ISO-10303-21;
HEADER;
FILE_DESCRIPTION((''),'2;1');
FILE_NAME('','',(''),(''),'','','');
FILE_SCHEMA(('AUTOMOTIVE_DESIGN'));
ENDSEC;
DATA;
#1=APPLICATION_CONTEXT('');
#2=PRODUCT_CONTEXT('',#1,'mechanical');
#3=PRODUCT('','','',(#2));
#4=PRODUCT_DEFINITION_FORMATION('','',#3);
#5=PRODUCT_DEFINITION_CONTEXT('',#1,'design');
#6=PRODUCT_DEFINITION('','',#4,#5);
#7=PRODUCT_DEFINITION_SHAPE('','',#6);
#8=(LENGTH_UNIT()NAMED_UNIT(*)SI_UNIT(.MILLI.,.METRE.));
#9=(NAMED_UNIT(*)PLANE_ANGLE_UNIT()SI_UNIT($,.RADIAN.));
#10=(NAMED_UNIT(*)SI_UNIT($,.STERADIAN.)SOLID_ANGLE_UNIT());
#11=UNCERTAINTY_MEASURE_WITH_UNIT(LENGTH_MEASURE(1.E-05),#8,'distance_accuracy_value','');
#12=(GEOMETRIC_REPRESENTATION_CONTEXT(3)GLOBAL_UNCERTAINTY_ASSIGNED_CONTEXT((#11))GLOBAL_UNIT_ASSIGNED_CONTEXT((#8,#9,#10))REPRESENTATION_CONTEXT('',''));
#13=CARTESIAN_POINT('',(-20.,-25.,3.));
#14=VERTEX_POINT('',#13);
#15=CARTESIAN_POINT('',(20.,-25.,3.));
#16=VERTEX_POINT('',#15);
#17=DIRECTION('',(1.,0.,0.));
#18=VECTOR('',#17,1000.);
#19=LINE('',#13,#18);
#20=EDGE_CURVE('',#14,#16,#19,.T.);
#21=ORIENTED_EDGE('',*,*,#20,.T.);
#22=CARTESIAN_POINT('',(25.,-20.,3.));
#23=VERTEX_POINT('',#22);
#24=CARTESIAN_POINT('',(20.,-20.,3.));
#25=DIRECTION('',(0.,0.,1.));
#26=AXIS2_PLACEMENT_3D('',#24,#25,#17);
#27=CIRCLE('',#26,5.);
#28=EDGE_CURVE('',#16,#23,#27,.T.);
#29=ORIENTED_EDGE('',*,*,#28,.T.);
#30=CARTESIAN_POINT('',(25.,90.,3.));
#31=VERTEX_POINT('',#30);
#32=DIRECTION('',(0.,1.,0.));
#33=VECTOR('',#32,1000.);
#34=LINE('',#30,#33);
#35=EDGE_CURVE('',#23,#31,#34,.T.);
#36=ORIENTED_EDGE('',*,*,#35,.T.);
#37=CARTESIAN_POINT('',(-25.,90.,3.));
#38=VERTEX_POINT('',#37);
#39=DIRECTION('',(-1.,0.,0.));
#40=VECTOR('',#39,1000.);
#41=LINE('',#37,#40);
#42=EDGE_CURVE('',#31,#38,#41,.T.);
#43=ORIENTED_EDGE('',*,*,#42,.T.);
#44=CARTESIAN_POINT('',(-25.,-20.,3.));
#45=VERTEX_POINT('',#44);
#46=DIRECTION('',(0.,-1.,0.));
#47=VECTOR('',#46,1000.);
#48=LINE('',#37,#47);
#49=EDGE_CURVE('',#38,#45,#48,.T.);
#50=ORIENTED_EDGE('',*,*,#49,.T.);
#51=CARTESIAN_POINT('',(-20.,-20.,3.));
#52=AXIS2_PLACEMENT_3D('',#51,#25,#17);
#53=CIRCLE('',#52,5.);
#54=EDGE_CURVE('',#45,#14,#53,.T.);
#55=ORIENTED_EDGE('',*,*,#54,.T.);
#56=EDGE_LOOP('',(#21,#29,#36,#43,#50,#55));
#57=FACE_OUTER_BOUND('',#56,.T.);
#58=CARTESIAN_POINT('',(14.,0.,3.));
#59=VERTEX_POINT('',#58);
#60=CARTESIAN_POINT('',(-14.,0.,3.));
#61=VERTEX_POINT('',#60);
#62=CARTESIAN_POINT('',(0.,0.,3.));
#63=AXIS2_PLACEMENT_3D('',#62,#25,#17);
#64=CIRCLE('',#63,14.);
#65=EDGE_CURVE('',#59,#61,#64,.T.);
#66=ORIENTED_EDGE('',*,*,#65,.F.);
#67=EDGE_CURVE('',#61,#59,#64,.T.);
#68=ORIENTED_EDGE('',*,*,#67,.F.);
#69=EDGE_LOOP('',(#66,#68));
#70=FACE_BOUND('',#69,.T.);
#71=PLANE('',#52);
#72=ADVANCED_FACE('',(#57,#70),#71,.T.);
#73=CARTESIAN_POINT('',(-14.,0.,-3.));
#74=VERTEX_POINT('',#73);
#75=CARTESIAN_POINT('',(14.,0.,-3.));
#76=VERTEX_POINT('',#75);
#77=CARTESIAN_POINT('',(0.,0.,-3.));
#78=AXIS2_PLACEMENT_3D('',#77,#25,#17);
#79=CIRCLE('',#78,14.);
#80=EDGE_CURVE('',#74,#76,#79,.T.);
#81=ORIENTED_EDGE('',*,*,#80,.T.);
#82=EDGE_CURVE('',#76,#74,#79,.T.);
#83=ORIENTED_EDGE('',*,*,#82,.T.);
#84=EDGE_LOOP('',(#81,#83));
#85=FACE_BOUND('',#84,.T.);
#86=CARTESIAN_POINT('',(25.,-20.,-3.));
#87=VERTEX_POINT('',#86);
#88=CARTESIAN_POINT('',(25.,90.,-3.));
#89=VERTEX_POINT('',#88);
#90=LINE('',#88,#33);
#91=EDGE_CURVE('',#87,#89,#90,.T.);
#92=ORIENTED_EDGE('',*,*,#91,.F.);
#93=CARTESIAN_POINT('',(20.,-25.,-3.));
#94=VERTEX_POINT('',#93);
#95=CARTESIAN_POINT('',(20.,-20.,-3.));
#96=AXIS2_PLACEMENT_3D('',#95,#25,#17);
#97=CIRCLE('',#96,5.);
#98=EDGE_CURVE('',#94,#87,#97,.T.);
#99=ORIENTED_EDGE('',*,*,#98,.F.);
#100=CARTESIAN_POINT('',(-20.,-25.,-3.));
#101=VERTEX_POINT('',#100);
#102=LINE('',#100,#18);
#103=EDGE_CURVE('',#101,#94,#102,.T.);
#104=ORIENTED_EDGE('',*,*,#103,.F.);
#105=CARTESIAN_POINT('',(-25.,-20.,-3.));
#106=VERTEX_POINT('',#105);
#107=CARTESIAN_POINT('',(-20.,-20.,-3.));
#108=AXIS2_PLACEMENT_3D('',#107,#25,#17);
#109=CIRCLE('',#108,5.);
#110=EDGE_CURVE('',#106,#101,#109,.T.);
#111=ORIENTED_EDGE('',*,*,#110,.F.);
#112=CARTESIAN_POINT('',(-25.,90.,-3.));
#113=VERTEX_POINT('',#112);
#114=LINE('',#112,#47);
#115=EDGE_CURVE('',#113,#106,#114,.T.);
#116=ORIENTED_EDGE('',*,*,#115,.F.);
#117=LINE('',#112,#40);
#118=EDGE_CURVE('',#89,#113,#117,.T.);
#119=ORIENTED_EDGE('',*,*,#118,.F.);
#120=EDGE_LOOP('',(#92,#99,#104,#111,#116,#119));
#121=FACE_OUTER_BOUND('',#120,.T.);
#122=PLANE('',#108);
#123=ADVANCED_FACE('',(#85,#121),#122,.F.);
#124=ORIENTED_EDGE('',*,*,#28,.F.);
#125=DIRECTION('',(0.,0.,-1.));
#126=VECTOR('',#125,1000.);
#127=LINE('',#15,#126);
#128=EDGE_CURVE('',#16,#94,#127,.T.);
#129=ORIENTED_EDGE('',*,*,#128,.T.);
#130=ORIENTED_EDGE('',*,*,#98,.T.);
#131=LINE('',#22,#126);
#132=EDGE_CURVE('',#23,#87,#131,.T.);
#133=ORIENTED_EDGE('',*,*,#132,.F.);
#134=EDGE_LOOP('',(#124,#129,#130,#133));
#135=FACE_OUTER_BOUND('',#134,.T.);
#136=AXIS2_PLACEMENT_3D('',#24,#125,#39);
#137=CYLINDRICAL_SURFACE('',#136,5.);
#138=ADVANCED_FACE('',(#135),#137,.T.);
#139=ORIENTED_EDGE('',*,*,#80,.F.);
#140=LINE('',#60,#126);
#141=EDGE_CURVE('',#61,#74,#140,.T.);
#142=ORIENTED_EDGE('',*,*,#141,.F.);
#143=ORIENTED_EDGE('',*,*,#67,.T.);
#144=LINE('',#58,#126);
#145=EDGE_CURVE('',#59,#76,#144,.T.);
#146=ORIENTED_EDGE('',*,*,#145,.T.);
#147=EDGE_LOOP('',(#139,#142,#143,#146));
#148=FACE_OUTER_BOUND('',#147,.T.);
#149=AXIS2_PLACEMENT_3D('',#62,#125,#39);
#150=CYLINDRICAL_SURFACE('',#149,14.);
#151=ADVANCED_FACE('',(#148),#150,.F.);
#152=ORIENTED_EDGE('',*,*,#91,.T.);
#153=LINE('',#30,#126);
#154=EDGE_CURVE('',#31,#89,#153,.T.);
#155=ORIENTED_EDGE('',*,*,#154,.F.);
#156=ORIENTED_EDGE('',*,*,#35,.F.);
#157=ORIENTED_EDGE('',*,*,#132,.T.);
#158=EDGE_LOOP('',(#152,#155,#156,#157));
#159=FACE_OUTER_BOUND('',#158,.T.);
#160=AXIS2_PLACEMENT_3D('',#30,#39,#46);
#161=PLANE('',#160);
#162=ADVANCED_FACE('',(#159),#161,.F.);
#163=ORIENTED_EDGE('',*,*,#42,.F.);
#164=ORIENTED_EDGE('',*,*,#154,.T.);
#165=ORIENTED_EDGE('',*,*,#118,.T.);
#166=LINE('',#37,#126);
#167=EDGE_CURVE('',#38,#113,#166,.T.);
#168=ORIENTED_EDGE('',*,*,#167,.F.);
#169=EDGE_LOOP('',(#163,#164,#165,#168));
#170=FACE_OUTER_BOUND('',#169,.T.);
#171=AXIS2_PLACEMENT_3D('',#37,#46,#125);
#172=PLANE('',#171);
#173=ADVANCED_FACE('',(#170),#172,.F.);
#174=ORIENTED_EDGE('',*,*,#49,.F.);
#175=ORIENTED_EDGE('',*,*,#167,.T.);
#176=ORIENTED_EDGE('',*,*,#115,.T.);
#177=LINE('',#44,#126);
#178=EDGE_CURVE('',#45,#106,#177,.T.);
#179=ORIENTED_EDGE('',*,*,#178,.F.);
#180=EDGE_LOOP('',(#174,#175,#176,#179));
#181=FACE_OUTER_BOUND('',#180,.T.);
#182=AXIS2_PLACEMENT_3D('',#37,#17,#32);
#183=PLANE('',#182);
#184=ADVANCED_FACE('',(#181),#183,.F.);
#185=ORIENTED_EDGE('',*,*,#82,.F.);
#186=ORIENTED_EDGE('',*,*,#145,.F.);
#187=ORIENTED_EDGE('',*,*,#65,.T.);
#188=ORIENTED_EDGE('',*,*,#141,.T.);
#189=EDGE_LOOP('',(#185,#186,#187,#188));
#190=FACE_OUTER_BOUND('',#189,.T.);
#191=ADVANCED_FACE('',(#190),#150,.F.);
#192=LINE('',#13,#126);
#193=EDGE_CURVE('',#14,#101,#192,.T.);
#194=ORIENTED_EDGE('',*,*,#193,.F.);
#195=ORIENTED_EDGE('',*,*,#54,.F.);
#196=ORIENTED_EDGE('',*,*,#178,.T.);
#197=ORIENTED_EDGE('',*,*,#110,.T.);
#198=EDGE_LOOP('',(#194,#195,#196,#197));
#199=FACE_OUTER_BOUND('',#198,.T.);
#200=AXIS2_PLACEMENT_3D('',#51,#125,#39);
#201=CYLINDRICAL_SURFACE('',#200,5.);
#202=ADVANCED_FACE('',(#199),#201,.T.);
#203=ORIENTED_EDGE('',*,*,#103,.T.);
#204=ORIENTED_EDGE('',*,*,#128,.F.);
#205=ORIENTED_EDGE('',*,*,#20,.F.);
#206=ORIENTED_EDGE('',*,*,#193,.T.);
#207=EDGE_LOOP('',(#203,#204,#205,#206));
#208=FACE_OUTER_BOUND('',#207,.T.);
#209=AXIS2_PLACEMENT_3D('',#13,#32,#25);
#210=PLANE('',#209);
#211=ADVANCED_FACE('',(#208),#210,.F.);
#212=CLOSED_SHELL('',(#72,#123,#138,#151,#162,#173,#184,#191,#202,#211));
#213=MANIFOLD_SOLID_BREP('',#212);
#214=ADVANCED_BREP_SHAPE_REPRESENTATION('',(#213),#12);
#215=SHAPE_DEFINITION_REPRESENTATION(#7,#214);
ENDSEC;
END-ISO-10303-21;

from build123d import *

# Parameters (mm, degrees)
SKETCH1_R           = 14
BOSS_EXTRUDE1_DEPTH = 3


with BuildPart() as part:
    # Sketch1 → Boss-Extrude1 (new, symmetric)
    with BuildSketch(Plane.XY):
        with BuildLine():
            Line((-25, 90), (25, 90))
            Line((25, 90), (25, -20))
            ThreePointArc((25, -20), (23.535533906, -23.535533906), (20, -25))
            Line((20, -25), (-20, -25))
            ThreePointArc((-20, -25), (-23.535533906, -23.535533906), (-25, -20))
            Line((-25, -20), (-25, 90))
        make_face()
        Circle(SKETCH1_R, mode=Mode.SUBTRACT)
    extrude(amount=BOSS_EXTRUDE1_DEPTH, both=True)


solid = part.part
